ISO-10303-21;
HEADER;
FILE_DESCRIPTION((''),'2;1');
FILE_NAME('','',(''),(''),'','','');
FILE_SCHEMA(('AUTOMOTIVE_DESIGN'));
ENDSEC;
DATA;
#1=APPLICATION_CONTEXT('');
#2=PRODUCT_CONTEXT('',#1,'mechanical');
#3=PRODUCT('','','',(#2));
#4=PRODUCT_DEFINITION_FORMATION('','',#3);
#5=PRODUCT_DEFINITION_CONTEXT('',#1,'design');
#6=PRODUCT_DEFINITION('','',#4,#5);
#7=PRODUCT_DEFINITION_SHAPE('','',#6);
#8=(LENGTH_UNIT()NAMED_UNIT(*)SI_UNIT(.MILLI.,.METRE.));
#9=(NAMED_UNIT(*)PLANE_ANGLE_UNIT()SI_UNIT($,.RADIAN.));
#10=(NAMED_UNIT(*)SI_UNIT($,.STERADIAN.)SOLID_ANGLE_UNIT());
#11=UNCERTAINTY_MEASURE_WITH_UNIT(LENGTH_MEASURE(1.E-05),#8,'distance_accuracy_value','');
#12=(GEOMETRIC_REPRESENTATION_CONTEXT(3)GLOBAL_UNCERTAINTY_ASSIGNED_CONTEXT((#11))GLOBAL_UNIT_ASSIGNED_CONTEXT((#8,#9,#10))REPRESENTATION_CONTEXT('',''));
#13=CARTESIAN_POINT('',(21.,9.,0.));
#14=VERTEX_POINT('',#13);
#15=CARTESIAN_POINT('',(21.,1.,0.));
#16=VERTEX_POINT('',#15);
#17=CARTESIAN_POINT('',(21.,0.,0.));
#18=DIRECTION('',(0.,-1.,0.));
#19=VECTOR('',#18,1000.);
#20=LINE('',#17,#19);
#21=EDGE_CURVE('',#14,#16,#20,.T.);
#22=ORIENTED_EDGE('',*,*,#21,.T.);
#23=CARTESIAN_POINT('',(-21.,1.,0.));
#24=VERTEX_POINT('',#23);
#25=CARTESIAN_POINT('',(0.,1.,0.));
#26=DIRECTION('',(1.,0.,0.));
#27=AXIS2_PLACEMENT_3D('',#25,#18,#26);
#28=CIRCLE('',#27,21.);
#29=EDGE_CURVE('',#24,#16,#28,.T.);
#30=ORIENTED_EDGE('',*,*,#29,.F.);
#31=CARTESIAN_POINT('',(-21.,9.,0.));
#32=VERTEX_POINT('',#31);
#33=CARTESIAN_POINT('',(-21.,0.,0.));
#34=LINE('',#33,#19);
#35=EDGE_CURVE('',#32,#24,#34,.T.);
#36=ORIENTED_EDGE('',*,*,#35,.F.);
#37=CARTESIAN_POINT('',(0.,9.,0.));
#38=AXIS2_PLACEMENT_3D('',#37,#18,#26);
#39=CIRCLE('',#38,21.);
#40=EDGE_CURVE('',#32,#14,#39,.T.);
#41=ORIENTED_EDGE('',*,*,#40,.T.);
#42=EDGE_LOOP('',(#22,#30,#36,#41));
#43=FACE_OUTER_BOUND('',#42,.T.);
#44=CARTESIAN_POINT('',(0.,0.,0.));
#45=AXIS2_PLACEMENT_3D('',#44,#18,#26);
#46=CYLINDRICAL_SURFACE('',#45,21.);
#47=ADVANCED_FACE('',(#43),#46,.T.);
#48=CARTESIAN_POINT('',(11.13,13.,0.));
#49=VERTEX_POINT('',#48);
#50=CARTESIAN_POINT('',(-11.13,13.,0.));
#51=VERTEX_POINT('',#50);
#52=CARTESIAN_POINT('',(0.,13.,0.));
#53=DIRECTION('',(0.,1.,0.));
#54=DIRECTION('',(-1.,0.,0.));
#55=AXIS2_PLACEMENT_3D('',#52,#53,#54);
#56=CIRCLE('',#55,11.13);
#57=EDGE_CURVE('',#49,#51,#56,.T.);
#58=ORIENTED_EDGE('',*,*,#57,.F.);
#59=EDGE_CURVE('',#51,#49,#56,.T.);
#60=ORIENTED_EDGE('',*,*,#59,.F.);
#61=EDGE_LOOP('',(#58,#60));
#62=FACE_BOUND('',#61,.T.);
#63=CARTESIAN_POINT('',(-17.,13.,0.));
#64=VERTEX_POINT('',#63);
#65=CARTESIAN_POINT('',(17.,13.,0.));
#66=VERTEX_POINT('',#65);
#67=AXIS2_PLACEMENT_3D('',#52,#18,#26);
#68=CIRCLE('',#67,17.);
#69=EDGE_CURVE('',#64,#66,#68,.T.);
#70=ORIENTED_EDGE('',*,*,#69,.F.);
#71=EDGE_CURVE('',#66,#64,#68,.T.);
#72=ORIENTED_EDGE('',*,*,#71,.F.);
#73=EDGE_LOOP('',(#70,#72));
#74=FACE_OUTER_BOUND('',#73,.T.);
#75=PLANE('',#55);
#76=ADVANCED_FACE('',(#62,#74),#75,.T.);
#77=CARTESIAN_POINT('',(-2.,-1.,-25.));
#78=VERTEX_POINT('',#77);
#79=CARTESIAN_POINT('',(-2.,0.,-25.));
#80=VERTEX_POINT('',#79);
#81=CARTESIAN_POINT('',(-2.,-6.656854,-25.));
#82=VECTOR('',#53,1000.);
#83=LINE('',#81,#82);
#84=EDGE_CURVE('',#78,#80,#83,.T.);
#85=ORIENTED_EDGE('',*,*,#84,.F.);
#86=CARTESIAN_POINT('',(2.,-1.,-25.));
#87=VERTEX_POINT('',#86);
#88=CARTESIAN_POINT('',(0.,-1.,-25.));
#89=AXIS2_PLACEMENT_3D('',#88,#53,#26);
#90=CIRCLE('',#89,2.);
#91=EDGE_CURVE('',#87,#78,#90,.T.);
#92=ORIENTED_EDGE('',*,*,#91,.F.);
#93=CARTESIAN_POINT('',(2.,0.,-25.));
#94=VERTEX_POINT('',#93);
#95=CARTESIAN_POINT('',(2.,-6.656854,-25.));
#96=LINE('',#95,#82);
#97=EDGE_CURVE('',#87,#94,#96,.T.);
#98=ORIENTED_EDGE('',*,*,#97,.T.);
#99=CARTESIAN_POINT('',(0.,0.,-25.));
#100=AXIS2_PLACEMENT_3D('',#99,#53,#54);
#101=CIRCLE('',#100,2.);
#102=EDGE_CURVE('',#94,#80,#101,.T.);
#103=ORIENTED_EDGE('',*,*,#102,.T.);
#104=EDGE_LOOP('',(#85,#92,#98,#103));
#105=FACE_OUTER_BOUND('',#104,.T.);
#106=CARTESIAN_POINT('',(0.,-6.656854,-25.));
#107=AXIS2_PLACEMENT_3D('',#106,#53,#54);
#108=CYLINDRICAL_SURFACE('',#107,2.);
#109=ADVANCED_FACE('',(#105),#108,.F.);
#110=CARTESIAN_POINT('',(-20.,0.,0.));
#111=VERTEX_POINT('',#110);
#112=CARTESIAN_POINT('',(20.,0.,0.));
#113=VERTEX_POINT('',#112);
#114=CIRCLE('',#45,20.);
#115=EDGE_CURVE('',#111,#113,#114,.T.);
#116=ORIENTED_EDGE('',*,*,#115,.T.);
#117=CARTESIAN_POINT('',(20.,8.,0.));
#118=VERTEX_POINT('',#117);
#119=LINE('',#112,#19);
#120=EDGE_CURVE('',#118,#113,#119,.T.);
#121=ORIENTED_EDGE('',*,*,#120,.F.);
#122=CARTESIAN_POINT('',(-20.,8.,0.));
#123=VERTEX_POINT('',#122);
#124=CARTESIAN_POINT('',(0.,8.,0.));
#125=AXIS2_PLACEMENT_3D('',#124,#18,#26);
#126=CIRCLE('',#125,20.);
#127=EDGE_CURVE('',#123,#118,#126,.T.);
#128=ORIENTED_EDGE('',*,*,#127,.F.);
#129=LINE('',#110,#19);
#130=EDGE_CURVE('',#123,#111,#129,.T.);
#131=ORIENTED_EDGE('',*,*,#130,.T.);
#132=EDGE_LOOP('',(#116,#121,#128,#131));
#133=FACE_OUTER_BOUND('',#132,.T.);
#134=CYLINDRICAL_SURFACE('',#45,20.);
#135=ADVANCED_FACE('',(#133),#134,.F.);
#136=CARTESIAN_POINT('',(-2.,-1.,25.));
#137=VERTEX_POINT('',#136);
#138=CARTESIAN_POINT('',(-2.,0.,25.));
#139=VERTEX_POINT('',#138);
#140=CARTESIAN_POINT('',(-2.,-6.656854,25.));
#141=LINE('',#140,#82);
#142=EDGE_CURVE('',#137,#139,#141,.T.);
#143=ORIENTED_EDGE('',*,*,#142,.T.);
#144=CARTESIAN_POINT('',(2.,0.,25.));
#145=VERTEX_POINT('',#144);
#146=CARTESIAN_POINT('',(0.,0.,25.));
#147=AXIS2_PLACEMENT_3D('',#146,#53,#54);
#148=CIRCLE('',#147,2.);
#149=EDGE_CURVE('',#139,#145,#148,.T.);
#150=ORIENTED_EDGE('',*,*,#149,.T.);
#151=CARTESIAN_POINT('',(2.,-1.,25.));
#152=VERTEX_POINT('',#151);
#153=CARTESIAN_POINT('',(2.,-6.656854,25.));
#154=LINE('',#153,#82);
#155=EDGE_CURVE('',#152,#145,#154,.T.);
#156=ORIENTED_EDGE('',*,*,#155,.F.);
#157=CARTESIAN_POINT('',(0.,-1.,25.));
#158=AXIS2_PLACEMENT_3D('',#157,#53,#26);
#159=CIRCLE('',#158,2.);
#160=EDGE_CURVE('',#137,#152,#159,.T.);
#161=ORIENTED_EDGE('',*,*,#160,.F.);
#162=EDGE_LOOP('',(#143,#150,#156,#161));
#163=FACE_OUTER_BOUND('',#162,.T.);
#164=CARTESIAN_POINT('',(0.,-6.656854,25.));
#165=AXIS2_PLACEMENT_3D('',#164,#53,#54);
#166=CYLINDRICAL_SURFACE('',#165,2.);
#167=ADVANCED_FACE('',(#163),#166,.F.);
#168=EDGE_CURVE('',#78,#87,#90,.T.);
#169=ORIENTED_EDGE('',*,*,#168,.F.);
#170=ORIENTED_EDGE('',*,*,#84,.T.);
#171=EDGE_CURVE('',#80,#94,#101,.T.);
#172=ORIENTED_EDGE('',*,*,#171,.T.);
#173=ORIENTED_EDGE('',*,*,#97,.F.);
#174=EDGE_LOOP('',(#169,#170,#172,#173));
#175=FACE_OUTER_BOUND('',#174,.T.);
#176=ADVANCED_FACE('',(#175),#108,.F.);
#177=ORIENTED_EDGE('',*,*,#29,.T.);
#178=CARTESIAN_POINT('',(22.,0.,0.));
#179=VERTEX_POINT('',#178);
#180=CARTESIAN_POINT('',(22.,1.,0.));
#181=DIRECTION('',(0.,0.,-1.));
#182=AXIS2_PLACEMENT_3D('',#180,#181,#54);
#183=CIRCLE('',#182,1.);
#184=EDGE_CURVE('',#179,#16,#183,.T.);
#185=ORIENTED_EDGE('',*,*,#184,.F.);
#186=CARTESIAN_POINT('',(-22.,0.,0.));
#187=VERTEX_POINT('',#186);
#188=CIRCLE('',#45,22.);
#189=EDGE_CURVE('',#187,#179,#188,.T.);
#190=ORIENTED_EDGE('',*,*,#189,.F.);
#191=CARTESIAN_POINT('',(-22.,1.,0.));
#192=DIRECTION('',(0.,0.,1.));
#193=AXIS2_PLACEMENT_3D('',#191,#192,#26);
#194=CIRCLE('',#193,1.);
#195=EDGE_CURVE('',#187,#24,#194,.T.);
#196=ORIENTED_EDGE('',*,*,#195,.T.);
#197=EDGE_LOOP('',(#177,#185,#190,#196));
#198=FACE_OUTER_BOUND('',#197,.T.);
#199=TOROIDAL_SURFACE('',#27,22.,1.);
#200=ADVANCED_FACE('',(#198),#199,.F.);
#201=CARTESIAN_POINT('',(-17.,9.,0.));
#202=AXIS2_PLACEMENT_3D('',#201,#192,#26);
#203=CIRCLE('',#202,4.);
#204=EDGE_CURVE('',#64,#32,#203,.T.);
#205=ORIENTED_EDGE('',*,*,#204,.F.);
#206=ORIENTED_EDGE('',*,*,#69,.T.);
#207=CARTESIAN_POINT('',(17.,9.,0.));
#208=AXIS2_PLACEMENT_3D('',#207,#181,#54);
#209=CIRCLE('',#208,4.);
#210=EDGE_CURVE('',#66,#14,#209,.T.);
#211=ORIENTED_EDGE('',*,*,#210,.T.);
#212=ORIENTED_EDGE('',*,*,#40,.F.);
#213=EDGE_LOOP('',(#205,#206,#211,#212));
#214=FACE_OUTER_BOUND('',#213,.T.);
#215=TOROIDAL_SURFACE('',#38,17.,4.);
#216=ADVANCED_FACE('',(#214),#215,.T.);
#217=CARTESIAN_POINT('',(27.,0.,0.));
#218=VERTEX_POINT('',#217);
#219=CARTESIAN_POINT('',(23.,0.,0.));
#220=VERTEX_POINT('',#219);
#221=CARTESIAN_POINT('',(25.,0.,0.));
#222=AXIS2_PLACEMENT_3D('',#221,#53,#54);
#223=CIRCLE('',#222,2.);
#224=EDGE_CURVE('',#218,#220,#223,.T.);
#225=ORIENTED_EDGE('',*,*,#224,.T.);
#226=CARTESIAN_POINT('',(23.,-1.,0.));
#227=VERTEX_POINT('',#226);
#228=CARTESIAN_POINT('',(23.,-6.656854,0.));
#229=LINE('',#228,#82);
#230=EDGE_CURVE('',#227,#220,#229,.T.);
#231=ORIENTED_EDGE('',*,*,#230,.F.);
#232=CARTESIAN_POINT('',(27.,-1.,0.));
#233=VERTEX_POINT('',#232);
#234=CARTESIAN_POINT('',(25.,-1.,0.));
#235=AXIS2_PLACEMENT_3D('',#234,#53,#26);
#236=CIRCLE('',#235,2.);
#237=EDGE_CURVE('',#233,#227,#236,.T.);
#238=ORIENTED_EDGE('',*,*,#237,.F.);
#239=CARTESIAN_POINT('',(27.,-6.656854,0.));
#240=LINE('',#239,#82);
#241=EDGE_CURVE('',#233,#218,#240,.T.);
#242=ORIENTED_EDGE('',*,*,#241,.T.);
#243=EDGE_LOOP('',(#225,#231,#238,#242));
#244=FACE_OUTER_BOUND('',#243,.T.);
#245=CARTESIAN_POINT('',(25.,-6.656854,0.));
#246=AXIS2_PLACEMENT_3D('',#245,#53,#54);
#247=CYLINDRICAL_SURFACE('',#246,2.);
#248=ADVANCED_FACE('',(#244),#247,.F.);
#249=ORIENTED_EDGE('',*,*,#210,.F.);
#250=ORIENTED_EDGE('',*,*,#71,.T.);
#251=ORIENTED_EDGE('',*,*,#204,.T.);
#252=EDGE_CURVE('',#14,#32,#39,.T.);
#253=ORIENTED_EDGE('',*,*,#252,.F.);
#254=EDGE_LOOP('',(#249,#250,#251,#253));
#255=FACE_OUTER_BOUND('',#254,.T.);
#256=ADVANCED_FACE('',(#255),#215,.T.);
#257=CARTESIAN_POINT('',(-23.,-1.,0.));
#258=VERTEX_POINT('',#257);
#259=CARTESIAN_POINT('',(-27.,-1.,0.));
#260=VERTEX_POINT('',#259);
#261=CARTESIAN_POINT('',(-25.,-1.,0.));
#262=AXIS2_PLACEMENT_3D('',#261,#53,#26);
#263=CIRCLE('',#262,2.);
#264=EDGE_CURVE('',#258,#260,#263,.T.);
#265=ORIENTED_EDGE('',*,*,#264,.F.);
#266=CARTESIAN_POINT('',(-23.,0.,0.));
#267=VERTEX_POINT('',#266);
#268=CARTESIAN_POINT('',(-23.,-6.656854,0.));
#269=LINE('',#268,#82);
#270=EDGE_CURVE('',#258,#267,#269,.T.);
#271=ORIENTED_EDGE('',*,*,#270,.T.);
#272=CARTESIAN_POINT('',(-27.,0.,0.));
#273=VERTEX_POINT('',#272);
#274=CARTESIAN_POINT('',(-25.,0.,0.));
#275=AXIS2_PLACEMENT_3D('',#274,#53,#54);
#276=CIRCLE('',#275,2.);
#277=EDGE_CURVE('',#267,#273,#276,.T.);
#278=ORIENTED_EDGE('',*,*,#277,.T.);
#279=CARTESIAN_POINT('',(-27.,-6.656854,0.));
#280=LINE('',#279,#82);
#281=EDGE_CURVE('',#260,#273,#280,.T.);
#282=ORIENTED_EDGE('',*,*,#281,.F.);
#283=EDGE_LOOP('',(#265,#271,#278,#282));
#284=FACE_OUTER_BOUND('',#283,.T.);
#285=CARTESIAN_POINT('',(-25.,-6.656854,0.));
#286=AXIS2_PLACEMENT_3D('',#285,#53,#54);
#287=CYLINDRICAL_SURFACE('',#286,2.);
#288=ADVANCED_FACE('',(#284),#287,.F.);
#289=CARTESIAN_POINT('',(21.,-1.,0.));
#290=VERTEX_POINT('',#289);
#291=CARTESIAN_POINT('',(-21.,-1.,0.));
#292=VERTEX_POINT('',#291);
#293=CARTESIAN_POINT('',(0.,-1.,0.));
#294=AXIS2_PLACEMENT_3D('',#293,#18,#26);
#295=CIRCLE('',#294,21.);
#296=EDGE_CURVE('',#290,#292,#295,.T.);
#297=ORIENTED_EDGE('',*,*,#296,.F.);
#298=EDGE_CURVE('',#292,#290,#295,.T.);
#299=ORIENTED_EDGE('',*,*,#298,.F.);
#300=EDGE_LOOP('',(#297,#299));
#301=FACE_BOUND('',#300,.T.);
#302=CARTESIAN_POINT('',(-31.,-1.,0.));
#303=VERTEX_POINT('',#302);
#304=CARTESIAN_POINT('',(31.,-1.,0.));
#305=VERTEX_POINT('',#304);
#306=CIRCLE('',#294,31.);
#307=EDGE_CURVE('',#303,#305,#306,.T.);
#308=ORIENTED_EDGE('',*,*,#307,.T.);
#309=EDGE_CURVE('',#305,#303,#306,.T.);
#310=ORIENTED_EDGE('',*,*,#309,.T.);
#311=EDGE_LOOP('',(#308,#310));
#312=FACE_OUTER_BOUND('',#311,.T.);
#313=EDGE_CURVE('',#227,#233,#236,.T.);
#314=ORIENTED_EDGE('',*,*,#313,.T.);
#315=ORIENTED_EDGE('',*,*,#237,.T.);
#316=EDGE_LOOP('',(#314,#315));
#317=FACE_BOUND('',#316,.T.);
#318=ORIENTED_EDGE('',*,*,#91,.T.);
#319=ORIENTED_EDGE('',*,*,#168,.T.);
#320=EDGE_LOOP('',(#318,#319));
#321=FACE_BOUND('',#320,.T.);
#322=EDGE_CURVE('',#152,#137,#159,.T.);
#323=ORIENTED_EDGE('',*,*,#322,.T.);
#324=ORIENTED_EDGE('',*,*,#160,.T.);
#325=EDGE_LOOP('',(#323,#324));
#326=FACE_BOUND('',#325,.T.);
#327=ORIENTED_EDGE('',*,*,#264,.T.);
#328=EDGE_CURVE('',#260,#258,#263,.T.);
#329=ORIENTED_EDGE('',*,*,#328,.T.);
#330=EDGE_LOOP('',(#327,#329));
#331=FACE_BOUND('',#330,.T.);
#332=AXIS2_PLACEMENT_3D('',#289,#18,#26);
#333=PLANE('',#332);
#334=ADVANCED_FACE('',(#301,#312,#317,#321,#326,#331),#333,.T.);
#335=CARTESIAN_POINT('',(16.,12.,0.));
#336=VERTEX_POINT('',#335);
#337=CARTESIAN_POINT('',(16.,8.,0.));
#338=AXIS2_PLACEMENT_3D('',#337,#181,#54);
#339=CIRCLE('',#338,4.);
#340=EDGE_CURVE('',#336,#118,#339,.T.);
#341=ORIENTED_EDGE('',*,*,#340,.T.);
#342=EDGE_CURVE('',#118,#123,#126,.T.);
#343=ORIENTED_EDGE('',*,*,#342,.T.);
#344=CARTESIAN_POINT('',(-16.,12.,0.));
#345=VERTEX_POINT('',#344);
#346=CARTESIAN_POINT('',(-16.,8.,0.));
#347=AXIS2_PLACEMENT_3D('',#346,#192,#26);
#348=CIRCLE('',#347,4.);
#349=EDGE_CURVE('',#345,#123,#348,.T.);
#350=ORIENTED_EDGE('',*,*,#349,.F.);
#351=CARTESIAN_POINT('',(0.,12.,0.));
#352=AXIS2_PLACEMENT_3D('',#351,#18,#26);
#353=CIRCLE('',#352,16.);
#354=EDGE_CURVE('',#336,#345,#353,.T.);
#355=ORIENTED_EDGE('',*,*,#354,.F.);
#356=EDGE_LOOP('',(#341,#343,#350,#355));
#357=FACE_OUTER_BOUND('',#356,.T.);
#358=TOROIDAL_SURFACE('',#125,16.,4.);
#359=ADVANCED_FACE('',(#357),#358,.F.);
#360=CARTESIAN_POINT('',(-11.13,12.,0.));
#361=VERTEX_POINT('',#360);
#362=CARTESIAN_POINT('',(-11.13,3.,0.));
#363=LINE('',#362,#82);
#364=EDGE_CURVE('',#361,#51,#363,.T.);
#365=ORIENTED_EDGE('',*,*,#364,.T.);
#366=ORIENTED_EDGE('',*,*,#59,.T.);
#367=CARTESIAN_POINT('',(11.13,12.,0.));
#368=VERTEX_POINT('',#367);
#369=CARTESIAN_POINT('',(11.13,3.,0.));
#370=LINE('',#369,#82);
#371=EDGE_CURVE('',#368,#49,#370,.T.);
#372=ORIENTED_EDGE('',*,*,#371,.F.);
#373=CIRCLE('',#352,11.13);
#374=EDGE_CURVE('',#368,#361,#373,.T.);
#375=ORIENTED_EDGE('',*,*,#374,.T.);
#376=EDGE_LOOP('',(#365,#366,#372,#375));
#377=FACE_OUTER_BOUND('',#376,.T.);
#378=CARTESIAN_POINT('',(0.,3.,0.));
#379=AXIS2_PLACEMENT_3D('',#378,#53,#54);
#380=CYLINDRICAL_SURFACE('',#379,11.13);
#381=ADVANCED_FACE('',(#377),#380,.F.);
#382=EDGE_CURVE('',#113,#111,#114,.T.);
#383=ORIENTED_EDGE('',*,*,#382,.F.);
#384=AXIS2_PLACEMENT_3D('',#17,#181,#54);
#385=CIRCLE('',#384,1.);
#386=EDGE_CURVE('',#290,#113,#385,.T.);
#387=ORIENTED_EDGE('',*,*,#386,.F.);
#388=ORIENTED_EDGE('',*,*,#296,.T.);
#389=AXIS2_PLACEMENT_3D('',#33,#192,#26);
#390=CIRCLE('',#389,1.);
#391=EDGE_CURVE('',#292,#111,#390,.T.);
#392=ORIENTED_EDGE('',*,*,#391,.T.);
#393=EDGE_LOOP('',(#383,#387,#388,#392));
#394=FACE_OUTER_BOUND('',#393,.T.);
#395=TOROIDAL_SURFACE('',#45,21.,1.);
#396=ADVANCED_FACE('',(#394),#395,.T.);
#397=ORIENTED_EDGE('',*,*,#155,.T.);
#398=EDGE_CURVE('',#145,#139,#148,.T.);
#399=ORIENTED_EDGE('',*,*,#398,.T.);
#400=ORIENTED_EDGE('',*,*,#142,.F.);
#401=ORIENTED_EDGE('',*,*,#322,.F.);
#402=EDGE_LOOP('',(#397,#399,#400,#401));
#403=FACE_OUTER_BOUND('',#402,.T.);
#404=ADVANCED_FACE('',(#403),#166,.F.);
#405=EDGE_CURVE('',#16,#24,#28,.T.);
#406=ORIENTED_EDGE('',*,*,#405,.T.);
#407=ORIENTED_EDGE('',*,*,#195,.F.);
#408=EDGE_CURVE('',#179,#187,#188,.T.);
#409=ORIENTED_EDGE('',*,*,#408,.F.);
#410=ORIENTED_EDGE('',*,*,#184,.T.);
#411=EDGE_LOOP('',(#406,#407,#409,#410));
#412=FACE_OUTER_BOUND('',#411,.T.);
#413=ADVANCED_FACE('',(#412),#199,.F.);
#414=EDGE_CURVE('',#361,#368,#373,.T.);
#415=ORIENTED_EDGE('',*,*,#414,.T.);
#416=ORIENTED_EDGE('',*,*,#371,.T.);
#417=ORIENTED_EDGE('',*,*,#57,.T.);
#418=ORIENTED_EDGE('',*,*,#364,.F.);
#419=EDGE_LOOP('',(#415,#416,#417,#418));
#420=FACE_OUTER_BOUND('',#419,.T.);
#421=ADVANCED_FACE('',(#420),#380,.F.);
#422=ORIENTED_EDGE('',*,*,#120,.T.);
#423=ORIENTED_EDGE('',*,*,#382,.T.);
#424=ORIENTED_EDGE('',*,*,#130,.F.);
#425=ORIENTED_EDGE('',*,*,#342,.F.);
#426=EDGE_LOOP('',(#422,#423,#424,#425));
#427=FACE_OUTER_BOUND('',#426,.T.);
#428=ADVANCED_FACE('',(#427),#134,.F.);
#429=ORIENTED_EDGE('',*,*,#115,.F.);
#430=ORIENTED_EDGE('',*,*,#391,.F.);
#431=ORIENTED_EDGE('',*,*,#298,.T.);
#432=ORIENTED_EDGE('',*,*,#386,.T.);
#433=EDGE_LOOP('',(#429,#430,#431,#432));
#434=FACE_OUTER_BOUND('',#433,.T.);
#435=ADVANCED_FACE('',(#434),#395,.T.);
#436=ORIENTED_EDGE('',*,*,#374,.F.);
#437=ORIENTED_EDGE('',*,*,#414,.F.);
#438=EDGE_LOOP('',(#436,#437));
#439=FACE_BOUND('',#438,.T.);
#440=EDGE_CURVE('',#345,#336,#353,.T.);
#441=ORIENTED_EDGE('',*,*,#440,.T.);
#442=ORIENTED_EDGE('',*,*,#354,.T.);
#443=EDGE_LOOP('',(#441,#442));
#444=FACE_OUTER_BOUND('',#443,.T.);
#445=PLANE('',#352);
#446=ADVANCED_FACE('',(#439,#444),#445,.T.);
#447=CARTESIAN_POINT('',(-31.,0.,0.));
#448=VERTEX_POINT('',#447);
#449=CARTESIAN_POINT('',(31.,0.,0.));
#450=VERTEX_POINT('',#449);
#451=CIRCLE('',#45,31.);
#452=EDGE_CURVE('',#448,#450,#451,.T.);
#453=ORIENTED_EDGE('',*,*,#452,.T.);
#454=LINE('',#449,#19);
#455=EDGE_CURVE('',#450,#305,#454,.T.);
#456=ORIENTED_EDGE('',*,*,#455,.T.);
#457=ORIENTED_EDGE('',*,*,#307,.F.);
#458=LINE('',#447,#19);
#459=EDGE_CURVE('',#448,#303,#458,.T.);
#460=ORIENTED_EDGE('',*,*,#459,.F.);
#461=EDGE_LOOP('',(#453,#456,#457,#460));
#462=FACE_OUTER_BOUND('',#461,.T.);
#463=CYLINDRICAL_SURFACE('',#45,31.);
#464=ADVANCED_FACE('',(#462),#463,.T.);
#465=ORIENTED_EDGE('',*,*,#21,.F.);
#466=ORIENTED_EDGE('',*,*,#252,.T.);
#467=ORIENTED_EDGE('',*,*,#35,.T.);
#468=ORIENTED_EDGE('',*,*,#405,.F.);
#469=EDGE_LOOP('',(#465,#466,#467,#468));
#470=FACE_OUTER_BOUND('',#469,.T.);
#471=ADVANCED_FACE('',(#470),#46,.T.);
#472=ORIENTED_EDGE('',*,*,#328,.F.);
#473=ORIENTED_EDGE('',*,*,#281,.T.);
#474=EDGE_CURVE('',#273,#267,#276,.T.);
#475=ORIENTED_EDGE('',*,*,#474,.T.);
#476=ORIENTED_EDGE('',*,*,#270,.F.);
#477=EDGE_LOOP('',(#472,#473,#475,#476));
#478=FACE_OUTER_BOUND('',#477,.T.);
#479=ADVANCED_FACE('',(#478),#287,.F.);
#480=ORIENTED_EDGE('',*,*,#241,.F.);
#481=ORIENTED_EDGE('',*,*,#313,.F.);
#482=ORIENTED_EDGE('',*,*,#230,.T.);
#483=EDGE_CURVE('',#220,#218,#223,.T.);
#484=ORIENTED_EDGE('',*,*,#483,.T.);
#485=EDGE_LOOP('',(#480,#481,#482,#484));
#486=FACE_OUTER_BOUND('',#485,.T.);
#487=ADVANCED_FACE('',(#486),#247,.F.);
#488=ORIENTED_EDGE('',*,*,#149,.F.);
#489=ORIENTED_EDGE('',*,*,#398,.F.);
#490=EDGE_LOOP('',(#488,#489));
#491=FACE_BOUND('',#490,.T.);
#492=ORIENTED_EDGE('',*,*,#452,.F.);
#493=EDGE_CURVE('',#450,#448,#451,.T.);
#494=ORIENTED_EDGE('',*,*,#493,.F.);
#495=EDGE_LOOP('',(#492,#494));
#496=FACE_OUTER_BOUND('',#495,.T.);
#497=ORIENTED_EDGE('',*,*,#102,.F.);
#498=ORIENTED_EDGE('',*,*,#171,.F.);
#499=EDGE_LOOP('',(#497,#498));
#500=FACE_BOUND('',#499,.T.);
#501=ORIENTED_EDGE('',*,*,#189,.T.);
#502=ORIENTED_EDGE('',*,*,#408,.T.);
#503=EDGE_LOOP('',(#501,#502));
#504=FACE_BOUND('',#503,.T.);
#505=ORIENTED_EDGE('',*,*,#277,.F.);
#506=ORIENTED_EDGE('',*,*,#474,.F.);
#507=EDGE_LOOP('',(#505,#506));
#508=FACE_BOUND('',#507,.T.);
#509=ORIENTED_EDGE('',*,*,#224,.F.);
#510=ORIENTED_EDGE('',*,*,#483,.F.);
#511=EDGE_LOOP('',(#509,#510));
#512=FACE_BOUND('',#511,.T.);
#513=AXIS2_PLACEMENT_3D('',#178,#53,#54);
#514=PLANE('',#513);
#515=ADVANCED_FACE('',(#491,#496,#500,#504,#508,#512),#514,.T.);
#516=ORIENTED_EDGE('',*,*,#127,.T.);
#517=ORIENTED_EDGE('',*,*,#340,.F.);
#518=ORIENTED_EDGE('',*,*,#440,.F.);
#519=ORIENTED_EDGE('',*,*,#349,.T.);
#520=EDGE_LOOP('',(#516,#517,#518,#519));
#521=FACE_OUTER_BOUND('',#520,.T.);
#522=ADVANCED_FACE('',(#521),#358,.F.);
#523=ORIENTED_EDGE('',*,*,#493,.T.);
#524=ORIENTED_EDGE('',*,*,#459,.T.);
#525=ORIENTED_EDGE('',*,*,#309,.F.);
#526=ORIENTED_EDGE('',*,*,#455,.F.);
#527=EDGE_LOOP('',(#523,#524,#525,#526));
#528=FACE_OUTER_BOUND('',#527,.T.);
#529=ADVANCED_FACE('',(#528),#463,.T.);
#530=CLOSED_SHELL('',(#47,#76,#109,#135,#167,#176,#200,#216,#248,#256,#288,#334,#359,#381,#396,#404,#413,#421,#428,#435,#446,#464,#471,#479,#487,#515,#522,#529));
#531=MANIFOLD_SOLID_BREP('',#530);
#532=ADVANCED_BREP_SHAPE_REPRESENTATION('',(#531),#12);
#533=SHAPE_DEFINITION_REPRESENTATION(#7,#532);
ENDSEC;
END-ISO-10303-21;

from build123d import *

# Parameters (mm, degrees)
SKETCH_2_R          = 2
CUT_EXTRUDE_1_DEPTH = 1
SKETCH_3_R          = 11.13
CUT_EXTRUDE_2_DEPTH = 10


with BuildPart() as part:
    # 草图1 → 旋转3 (revolve)
    with BuildSketch(Plane.XY):
        with BuildLine():
            Line((0, 13), (0, 12))
            Line((0, 12), (16, 12))
            ThreePointArc((16, 12), (18.828427125, 10.828427125), (20, 8))
            Line((20, 8), (20, 0))
            ThreePointArc((20, 0), (20.292893219, -0.707106781), (21, -1))
            Line((21, -1), (31, -1))
            Line((31, -1), (31, 0))
            Line((31, 0), (22, 0))
            ThreePointArc((22, 0), (21.292893219, 0.292893219), (21, 1))
            Line((21, 1), (21, 9))
            ThreePointArc((21, 9), (19.828427125, 11.828427125), (17, 13))
            Line((17, 13), (0, 13))
        make_face()
    revolve(axis=Axis((0, 0, 0), (0, 1, 0)))

    # 草图2 → 切除-拉伸1 (cut)
    with BuildSketch(Plane(origin=(0, 0, 0), x_dir=(1, 0, 0), z_dir=(0, 1, 0))):
        with Locations(Location((0, 25, 0), (0, 0, 180))):
            Circle(SKETCH_2_R)
        with Locations(Location((25, 0, 0), (0, 0, 180))):
            Circle(SKETCH_2_R)
        with Locations(Location((0, -25, 0), (0, 0, 180))):
            Circle(SKETCH_2_R)
        with Locations(Location((-25, 0, 0), (0, 0, 180))):
            Circle(SKETCH_2_R)
    extrude(amount=-CUT_EXTRUDE_1_DEPTH, mode=Mode.SUBTRACT)

    # 草图3 → 切除-拉伸2 (cut)
    with BuildSketch(Plane(origin=(0, 13, 0), x_dir=(1, 0, 0), z_dir=(0, 1, 0))):
        with Locations(Location((0, 0, 0), (0, 0, 180))):
            Circle(SKETCH_3_R)
    extrude(amount=-CUT_EXTRUDE_2_DEPTH, mode=Mode.SUBTRACT)


solid = part.part
